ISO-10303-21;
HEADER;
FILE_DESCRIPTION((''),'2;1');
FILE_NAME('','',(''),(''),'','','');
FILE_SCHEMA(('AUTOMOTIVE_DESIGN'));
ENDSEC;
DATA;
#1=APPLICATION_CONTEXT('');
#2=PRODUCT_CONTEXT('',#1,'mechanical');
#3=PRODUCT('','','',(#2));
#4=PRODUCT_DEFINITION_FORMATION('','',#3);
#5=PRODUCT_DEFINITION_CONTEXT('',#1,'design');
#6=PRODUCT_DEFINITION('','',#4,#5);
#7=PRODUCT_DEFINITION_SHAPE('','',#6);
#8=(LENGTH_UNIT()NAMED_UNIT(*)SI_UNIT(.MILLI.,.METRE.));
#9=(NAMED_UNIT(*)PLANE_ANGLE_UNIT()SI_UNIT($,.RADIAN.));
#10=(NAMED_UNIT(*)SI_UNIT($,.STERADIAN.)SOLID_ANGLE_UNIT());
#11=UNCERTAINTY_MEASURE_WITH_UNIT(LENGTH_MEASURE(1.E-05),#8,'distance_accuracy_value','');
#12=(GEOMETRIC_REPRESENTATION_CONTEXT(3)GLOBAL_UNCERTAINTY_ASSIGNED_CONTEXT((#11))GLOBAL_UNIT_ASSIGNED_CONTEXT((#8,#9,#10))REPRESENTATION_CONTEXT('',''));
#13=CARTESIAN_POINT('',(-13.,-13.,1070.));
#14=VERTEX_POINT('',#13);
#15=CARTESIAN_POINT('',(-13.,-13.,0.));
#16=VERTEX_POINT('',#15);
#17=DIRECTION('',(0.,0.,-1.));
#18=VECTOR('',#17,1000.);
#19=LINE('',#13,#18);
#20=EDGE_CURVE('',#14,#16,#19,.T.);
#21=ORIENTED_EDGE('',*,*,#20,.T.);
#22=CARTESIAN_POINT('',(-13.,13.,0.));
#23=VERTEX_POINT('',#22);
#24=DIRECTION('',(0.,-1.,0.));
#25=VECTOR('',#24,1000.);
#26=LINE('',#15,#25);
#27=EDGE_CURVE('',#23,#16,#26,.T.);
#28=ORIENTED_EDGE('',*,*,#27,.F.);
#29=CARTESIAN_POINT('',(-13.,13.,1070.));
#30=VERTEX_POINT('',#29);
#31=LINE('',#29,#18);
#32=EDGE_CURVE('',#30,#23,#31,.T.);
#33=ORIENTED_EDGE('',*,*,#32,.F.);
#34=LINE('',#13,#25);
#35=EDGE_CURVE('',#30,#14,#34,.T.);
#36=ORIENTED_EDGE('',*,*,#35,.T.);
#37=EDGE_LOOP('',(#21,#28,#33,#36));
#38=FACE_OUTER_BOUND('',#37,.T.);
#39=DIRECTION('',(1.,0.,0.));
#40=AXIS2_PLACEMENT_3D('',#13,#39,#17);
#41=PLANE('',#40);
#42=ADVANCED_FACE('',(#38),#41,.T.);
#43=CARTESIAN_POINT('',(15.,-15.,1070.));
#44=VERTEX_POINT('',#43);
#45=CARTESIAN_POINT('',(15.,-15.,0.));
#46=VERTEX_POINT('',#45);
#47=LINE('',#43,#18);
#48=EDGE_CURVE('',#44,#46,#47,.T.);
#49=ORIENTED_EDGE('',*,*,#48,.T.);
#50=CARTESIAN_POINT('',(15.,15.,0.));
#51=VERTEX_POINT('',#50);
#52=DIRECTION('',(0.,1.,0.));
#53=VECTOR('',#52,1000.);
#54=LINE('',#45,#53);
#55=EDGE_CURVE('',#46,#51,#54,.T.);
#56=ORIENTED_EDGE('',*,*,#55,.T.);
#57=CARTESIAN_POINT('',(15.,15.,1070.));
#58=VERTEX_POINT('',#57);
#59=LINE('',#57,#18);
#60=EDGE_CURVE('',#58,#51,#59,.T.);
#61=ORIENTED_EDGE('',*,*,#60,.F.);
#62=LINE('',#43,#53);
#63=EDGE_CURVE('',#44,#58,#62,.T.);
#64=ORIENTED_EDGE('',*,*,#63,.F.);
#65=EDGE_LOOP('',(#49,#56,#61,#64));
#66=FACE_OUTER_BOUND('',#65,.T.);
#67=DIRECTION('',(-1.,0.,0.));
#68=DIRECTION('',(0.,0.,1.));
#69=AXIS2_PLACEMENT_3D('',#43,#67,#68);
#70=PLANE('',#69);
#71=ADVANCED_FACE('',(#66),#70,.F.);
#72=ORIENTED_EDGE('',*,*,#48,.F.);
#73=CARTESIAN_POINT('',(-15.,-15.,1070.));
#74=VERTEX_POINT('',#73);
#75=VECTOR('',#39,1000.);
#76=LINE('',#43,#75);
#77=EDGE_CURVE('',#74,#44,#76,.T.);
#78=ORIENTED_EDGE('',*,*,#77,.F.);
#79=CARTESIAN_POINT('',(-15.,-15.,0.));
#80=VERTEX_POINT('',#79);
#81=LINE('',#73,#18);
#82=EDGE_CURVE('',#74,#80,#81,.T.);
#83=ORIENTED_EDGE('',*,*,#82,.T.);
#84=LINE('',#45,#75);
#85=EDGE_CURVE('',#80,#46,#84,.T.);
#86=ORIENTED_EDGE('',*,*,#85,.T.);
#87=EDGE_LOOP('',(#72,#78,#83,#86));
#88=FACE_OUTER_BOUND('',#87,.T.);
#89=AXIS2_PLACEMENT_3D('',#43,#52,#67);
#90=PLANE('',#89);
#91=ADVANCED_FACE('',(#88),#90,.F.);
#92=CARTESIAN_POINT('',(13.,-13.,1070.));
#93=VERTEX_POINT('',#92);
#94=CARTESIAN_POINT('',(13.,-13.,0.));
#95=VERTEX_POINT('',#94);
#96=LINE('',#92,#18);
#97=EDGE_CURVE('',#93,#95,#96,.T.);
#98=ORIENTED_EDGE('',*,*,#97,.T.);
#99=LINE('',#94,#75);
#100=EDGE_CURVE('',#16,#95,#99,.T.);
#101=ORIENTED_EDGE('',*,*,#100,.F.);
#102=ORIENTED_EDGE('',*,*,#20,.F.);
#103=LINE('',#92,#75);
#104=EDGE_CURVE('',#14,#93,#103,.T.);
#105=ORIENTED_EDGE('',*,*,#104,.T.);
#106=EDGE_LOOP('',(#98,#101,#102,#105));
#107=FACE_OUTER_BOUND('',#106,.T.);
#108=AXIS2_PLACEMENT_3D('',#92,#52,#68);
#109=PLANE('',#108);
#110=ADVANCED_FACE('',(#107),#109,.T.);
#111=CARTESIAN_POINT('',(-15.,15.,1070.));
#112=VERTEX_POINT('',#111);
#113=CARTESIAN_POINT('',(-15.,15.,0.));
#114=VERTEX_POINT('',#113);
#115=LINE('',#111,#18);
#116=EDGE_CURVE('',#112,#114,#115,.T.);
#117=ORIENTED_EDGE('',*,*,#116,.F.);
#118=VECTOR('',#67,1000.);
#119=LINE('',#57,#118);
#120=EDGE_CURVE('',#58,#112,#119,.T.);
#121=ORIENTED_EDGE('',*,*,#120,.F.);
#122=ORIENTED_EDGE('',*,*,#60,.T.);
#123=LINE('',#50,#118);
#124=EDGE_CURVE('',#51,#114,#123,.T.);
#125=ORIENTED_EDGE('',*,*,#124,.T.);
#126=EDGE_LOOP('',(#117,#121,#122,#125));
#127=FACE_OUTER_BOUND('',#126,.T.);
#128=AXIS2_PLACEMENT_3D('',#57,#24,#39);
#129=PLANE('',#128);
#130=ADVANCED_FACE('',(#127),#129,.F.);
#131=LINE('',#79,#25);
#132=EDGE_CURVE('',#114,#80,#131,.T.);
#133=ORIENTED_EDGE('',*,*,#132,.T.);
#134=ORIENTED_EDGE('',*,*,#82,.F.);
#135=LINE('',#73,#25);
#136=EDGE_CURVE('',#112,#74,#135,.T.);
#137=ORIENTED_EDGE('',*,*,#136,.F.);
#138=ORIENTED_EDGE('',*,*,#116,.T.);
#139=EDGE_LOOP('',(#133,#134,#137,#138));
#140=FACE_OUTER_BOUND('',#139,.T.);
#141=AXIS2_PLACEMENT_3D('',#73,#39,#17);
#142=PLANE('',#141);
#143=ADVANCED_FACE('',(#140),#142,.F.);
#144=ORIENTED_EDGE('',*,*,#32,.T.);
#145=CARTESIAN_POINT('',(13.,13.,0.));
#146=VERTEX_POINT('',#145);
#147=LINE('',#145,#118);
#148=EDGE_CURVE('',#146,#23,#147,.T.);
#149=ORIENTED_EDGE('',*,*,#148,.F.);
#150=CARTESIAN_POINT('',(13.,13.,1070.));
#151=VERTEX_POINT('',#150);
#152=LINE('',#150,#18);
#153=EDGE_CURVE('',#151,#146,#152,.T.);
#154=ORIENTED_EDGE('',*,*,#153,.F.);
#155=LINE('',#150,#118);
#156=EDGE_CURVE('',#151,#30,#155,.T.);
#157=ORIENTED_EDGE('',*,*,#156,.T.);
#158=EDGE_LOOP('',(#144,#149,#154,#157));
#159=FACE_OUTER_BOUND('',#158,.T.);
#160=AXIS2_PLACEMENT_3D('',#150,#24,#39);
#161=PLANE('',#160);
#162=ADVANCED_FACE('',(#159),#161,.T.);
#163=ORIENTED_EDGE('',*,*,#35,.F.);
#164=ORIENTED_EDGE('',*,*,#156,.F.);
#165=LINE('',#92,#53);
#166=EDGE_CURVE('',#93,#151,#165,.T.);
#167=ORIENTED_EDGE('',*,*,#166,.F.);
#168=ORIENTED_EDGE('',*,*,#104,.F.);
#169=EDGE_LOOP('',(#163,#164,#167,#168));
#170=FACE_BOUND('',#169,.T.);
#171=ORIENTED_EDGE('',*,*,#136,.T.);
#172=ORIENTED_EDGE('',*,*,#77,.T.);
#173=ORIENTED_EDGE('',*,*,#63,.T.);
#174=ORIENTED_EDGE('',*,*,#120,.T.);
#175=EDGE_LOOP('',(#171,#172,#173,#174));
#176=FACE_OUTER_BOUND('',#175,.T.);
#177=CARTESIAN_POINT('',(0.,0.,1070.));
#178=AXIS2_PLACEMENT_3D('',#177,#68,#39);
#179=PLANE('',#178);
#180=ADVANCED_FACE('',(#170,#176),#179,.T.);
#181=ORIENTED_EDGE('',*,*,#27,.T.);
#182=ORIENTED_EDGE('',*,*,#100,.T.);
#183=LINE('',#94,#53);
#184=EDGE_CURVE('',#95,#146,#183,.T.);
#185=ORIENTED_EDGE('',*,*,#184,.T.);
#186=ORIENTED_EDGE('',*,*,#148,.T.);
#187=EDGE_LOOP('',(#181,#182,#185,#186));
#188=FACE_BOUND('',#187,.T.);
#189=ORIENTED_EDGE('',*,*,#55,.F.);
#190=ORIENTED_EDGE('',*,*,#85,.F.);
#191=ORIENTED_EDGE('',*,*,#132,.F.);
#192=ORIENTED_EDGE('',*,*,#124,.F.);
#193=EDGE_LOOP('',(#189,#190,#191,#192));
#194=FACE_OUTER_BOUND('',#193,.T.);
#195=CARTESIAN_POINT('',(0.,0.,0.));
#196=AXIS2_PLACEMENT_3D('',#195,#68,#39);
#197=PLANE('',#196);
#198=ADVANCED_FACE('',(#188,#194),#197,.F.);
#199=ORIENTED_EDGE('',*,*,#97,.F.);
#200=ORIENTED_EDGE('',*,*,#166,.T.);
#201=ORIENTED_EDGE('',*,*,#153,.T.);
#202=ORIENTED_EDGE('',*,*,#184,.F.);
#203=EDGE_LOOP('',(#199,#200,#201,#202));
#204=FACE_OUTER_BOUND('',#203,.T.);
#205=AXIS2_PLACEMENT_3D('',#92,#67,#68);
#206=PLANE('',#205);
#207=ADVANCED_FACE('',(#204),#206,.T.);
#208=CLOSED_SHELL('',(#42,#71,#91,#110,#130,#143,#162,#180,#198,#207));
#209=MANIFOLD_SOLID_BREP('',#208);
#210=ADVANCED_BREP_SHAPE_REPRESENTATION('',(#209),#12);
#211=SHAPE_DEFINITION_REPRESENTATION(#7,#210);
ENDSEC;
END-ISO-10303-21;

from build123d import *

# Parameters (mm, degrees)
SKETCH_1_W      = 30
SKETCH_1_H      = 30
SKETCH_1_W_2    = 26
SKETCH_1_H_2    = 26
EXTRUDE_1_DEPTH = 1070


with BuildPart() as part:
    # 草图1 → 凸台-拉伸1 (new body)
    with BuildSketch(Plane.XY):
        Rectangle(SKETCH_1_W, SKETCH_1_H)
        Rectangle(SKETCH_1_W_2, SKETCH_1_H_2, mode=Mode.SUBTRACT)
    extrude(amount=EXTRUDE_1_DEPTH)


solid = part.part
